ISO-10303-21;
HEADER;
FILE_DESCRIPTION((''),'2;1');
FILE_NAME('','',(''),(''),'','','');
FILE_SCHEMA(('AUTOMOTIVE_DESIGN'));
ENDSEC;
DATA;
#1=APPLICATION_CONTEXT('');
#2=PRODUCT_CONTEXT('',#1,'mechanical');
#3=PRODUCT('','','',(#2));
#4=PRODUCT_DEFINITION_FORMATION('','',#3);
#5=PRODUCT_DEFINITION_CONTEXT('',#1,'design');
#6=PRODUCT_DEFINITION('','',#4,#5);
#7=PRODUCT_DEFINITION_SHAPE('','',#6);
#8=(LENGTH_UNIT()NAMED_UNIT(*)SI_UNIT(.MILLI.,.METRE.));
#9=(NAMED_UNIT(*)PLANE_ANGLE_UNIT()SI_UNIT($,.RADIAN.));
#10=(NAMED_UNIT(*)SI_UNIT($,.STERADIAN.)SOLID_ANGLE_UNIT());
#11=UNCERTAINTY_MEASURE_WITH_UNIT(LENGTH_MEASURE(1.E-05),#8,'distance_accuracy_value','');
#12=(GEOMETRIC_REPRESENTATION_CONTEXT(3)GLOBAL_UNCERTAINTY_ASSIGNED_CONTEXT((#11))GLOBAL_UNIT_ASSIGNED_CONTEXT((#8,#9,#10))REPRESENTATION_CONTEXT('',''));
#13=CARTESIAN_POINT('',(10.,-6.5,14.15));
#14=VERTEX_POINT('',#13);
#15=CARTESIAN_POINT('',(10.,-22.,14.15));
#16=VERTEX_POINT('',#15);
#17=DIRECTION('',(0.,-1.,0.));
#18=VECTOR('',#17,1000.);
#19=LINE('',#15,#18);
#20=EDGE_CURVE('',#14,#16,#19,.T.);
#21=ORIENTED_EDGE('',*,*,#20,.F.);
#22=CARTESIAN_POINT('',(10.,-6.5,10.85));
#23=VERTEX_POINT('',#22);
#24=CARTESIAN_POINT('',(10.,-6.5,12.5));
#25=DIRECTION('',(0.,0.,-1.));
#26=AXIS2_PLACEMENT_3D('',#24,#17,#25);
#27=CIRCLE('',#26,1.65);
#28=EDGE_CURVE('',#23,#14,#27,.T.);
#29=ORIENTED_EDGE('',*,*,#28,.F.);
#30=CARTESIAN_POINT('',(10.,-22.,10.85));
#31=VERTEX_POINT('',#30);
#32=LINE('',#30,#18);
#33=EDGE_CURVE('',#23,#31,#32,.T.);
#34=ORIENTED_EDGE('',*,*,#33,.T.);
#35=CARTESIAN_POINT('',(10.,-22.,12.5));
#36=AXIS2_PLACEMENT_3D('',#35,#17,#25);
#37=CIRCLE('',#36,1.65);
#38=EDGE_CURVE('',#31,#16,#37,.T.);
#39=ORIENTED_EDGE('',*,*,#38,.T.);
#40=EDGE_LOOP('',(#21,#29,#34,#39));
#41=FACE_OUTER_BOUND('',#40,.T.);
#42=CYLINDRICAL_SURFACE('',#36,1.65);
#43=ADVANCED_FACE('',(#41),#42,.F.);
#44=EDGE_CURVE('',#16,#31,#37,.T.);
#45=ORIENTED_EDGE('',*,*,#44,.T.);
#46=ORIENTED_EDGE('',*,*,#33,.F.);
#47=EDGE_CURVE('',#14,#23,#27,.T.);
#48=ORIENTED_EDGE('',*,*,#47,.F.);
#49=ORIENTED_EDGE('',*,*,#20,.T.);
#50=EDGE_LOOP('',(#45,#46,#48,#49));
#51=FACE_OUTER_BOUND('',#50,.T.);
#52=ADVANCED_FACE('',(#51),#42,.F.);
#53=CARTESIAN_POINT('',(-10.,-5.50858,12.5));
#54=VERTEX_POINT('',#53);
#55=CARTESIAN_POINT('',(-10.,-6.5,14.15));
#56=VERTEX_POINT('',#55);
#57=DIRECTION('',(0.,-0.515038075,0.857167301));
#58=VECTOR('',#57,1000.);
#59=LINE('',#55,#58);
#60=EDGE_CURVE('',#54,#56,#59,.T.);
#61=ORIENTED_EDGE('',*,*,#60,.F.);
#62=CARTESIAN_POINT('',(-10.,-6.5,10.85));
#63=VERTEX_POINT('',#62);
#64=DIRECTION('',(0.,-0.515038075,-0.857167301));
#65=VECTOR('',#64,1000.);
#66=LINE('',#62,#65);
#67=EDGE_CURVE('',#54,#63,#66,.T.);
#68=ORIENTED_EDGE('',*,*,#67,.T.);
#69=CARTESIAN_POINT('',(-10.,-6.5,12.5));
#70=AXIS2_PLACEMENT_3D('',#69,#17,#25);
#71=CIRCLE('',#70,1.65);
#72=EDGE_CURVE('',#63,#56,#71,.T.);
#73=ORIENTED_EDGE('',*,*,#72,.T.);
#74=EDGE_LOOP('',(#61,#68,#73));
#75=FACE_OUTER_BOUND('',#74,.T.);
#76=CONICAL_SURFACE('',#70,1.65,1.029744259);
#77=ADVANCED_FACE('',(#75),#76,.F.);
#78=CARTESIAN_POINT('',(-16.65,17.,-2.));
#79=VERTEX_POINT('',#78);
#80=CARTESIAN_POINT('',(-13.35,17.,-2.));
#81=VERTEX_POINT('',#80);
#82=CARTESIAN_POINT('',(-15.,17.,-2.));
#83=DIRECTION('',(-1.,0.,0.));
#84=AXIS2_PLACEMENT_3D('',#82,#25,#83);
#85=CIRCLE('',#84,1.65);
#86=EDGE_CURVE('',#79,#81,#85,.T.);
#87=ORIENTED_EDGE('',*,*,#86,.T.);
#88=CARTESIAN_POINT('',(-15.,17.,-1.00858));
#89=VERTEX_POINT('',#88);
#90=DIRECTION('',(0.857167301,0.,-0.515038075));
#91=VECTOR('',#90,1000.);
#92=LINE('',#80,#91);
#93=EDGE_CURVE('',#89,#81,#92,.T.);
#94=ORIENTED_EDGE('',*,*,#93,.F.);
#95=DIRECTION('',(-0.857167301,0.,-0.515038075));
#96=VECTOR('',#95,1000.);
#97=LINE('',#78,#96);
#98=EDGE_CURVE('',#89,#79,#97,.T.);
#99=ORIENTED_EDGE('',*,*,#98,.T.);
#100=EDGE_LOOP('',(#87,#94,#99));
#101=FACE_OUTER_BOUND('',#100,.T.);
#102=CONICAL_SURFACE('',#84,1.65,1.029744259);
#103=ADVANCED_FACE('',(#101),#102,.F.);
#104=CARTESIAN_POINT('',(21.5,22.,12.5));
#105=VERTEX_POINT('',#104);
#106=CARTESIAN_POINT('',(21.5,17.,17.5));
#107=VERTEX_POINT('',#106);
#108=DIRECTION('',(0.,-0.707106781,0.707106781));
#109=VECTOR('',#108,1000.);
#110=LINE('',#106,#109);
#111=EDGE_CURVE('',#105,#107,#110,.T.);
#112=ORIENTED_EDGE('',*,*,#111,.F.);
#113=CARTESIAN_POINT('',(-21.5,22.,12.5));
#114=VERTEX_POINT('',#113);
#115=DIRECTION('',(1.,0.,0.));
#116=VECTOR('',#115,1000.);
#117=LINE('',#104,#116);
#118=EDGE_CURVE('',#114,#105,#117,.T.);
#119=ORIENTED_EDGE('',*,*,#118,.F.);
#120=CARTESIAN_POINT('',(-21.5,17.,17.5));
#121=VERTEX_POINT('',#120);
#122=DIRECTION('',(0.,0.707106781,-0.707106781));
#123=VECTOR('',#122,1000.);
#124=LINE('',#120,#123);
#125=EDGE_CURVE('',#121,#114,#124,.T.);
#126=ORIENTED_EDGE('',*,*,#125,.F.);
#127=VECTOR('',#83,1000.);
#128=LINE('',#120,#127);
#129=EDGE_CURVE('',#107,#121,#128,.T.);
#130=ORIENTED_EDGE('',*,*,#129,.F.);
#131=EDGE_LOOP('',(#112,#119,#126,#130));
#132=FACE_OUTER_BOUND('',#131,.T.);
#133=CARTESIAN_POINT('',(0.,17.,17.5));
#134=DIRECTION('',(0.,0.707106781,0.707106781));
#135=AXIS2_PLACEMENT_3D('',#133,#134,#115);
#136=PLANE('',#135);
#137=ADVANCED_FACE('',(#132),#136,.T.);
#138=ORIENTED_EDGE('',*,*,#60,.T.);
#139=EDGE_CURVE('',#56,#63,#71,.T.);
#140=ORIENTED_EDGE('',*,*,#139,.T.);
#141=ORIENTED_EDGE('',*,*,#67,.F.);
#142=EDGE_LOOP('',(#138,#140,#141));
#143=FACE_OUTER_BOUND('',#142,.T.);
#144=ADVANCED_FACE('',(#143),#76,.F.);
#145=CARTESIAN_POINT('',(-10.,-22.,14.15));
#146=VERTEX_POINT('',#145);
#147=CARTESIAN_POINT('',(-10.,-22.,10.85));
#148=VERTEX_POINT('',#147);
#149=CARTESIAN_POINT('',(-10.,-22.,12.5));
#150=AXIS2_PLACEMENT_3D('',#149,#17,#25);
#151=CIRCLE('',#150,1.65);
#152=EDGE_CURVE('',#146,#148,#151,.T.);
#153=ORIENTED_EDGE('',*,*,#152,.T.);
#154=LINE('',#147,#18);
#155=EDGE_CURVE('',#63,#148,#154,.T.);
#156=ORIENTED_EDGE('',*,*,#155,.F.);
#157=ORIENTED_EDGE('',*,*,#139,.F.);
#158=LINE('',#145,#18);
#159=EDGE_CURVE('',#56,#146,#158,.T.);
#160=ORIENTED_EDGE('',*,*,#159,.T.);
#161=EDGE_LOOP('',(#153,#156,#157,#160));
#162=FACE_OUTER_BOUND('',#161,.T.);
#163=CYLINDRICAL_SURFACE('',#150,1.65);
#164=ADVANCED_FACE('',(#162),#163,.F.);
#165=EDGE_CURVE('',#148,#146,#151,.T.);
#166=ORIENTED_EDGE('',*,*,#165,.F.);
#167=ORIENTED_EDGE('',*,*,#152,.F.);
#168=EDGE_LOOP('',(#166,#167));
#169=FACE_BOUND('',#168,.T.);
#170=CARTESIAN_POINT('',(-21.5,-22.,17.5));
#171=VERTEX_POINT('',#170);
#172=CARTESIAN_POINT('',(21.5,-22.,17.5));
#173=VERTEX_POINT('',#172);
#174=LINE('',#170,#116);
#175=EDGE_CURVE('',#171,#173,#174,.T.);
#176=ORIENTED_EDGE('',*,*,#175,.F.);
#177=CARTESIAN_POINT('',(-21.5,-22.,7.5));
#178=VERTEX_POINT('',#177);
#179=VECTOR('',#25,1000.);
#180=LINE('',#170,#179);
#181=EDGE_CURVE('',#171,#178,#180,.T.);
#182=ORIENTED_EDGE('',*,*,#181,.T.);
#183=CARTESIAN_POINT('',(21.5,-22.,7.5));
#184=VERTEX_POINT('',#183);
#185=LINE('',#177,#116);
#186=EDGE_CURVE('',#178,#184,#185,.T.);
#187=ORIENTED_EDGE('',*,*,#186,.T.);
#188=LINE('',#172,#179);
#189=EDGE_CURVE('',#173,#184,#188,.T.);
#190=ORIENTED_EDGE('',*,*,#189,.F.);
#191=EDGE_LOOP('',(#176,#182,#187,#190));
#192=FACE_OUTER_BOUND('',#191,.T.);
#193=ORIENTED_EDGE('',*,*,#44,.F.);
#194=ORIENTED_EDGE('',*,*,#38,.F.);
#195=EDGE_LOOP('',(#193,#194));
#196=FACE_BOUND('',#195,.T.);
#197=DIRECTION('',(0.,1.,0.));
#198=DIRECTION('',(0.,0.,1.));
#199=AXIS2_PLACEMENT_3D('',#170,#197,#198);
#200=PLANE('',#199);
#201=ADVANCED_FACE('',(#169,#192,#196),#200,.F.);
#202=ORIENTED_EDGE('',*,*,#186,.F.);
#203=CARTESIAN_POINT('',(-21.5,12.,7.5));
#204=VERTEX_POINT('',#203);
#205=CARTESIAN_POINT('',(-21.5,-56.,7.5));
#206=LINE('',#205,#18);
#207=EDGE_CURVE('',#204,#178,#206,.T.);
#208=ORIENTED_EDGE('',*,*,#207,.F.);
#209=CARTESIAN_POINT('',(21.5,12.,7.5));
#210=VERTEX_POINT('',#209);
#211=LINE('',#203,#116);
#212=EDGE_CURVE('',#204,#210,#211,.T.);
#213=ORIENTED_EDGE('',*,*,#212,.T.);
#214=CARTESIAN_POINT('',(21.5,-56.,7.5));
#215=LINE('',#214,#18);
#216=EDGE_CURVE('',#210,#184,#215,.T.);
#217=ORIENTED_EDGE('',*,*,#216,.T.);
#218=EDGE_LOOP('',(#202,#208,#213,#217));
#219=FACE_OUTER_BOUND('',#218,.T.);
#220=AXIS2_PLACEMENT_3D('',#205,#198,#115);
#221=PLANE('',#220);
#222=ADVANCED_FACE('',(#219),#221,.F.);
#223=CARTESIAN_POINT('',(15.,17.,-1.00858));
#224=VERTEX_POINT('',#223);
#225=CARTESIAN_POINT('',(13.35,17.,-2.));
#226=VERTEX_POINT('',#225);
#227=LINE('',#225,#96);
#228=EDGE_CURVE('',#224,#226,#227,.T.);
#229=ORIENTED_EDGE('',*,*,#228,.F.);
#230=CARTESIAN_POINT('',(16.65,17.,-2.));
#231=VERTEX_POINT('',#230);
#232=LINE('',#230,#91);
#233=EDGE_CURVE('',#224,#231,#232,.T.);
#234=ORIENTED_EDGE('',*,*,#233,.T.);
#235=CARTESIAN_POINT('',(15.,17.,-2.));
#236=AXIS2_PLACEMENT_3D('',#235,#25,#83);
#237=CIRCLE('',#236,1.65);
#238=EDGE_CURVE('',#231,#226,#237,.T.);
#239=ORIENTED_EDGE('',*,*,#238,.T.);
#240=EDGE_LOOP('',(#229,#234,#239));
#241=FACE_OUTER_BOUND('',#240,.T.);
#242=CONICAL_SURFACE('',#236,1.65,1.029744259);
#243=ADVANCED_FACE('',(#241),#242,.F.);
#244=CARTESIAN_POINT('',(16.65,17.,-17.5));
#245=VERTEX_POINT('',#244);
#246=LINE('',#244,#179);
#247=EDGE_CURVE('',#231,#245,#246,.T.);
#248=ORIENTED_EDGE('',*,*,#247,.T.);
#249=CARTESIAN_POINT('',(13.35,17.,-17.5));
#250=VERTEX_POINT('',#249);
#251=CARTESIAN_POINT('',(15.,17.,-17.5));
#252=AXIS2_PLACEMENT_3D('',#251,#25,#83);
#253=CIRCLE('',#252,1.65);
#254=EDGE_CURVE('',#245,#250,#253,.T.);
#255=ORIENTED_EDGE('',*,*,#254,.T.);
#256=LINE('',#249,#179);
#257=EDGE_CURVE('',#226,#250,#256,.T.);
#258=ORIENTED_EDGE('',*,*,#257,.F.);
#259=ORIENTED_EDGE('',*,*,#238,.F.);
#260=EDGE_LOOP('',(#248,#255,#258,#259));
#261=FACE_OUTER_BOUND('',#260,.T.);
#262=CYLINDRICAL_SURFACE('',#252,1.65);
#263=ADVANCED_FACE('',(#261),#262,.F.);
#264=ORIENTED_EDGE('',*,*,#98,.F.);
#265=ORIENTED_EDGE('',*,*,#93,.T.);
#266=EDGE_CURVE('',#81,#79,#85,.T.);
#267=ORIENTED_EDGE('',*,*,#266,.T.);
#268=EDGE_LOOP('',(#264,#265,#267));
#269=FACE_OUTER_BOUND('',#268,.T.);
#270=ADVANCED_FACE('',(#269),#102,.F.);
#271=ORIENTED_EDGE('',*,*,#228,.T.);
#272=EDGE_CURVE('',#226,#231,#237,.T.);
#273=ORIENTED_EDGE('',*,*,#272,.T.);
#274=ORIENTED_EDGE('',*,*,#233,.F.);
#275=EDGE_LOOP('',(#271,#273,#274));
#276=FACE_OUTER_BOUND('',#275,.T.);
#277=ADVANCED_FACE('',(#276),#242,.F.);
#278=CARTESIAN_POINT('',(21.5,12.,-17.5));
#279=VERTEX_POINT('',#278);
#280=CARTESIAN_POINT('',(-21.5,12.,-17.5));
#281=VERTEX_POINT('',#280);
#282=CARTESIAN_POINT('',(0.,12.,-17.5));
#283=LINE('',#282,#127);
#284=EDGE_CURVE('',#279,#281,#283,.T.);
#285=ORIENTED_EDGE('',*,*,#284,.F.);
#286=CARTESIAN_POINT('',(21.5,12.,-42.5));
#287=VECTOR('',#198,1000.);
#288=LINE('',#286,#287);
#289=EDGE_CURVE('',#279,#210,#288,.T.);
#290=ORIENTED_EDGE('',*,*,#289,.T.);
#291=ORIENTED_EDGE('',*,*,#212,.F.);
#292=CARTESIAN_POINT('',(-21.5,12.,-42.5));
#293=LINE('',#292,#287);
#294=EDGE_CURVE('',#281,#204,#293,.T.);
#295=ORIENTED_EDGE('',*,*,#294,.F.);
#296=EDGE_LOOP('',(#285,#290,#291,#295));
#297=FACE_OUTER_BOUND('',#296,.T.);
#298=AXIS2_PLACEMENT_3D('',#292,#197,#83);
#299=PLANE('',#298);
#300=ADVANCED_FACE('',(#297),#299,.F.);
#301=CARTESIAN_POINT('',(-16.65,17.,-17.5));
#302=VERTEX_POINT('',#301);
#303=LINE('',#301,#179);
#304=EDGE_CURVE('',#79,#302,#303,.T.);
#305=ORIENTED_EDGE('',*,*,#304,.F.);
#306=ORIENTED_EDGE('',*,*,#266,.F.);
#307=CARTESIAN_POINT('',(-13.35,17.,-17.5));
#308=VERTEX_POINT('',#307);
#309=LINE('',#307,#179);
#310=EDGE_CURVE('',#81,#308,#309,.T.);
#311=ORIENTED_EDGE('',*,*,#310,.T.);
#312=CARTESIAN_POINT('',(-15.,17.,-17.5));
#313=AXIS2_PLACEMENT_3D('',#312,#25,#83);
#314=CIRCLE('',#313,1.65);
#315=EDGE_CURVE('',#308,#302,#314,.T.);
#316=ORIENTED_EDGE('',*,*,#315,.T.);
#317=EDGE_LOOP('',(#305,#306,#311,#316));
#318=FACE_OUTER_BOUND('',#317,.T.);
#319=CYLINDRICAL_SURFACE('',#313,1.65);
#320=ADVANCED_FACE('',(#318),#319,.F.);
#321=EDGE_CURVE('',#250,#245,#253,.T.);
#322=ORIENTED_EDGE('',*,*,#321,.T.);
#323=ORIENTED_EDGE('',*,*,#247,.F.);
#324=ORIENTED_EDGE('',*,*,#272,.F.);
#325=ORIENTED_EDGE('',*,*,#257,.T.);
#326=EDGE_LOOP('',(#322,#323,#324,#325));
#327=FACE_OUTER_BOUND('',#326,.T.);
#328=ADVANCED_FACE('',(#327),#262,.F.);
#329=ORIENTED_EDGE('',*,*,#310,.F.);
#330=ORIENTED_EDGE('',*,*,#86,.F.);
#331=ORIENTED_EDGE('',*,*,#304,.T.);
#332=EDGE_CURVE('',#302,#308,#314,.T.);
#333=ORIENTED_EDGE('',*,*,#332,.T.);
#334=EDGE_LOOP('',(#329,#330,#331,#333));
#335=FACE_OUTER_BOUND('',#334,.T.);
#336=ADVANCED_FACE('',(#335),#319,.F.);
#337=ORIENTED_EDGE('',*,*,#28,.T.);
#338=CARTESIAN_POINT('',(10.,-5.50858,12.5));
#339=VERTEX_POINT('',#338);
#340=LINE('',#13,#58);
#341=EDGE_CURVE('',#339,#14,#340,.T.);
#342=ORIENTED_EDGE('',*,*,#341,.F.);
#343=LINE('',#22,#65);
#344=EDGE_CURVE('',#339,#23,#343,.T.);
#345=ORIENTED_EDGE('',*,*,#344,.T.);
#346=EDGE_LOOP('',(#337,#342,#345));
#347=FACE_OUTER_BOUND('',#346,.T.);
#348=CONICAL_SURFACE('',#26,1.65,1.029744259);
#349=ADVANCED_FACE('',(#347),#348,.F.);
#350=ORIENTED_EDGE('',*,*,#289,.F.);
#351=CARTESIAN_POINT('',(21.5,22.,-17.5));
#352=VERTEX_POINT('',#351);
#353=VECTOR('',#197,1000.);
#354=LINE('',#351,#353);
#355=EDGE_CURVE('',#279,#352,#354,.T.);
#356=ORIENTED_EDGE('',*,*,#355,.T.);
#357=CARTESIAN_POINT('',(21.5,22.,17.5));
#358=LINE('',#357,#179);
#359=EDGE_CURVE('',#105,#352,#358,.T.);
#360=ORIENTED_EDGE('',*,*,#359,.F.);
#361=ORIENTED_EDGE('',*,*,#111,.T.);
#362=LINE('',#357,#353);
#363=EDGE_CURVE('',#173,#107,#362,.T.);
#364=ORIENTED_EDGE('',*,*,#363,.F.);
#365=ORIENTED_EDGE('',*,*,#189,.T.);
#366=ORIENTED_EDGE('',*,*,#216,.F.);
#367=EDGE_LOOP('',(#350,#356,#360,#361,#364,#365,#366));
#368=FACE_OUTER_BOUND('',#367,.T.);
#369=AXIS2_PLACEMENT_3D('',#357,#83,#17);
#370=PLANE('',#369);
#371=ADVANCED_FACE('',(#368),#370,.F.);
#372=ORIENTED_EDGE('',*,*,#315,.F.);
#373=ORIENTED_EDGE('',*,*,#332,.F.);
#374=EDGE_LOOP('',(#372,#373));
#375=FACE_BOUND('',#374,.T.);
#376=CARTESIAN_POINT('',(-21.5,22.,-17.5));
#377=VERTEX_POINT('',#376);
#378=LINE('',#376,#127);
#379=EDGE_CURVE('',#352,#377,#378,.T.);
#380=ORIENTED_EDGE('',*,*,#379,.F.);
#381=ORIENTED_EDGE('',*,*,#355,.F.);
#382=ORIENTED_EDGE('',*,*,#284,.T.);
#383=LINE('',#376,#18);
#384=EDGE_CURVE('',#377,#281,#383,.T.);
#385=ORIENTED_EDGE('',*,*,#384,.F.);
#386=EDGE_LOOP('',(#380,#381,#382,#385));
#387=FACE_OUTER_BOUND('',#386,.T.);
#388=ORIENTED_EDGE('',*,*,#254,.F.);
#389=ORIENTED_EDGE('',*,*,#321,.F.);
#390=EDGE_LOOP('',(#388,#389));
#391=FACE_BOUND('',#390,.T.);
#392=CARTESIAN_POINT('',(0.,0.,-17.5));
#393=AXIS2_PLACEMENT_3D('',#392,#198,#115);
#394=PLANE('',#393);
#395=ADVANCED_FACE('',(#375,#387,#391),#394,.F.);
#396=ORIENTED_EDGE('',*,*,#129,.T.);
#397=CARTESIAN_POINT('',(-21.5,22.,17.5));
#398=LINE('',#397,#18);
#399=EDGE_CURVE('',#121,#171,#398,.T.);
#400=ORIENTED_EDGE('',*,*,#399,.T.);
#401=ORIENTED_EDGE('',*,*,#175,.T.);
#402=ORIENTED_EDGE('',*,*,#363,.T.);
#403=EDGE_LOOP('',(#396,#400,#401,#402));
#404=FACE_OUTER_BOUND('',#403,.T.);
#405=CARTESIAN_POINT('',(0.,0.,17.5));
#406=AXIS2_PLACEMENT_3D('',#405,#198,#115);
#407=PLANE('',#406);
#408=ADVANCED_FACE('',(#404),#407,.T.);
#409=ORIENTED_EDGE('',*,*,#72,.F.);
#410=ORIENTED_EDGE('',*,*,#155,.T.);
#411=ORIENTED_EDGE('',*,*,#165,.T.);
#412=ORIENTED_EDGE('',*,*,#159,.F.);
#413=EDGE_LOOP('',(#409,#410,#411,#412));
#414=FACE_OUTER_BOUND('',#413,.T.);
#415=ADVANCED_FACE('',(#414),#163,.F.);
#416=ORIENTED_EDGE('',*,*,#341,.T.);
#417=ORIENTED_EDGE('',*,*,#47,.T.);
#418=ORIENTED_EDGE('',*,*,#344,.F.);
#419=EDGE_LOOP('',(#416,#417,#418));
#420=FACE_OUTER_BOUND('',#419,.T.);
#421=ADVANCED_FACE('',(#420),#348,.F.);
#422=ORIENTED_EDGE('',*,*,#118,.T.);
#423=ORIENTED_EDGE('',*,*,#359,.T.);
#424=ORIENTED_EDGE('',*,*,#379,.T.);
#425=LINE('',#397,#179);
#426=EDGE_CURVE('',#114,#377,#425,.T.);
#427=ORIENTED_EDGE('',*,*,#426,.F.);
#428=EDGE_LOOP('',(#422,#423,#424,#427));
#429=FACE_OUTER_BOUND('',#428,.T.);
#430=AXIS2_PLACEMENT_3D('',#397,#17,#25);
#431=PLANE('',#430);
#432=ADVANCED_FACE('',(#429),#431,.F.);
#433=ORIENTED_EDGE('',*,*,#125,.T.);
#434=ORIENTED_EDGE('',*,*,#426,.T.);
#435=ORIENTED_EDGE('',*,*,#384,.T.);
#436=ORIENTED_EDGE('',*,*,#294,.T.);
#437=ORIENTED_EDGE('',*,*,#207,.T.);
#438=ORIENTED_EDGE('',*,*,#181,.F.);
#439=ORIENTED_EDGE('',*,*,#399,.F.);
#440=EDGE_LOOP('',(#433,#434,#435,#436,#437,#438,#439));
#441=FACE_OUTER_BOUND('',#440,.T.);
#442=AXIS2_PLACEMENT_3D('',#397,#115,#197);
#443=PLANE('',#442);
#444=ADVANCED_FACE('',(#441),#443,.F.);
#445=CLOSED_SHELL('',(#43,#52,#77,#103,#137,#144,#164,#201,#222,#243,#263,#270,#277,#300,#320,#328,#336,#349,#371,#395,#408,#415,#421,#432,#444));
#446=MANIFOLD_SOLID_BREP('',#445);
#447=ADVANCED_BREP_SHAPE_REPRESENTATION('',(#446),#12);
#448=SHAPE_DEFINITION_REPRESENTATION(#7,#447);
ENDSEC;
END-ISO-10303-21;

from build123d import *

# Parameters (mm, degrees)
SKETCH_1_W             = 43
SKETCH_1_H             = 44
EXTRUDE_1_DEPTH        = 17.5
SKETCH_2_W             = 50
SKETCH_2_H             = 68
CUT_EXTRUDE_1_DEPTH    = 52.373631369
HOLE_WIZARD_M4_1_D     = 3.3
HOLE_WIZARD_M4_1_DEPTH = 15.5
HOLE_WIZARD_M4_1_TIP   = 0.991420021
CHAMFER_1_SIZE         = 5
HOLE_WIZARD_M4_2_D     = 3.3
HOLE_WIZARD_M4_2_DEPTH = 15.5
HOLE_WIZARD_M4_2_TIP   = 0.991420021


with BuildPart() as part:
    # 草图1 → 凸台-拉伸1 (new, symmetric)
    with BuildSketch(Plane.XY):
        Rectangle(SKETCH_1_W, SKETCH_1_H)
    extrude(amount=EXTRUDE_1_DEPTH, both=True)

    # 草图2 → 切除-拉伸1 (cut, through all)
    with BuildSketch(Plane(origin=(21.5, 0, 0), x_dir=(0, 0, -1), z_dir=(1, 0, 0))):
        with Locations((17.5, -22)):
            Rectangle(SKETCH_2_W, SKETCH_2_H)
    extrude(amount=-CUT_EXTRUDE_1_DEPTH, mode=Mode.SUBTRACT)

    # M4 螺纹孔1
    with Locations(Plane(origin=(0, 0, -17.5), x_dir=(-1, 0, 0), z_dir=(0, 0, -1))):
        with Locations((-15, 17), (15, 17)):
            Hole(HOLE_WIZARD_M4_1_D / 2, depth=HOLE_WIZARD_M4_1_DEPTH)
            with Locations((0, 0, -(HOLE_WIZARD_M4_1_DEPTH + HOLE_WIZARD_M4_1_TIP / 2))):  # 118° drill point
                Cone(0, HOLE_WIZARD_M4_1_D / 2, HOLE_WIZARD_M4_1_TIP, mode=Mode.SUBTRACT)

    # 倒角1
    chamfer_1_edges = [part.edges().sort_by_distance(p)[0] for p in [
        (0, 22, 17.5),
    ]]
    chamfer(chamfer_1_edges, length=CHAMFER_1_SIZE)

    # M4 螺纹孔2
    with Locations(Plane(origin=(0, -22, 0), x_dir=(-1, 0, 0), z_dir=(0, -1, 0))):
        with Locations((10, -12.5), (-10, -12.5)):
            Hole(HOLE_WIZARD_M4_2_D / 2, depth=HOLE_WIZARD_M4_2_DEPTH)
            with Locations((0, 0, -(HOLE_WIZARD_M4_2_DEPTH + HOLE_WIZARD_M4_2_TIP / 2))):  # 118° drill point
                Cone(0, HOLE_WIZARD_M4_2_D / 2, HOLE_WIZARD_M4_2_TIP, mode=Mode.SUBTRACT)


solid = part.part
